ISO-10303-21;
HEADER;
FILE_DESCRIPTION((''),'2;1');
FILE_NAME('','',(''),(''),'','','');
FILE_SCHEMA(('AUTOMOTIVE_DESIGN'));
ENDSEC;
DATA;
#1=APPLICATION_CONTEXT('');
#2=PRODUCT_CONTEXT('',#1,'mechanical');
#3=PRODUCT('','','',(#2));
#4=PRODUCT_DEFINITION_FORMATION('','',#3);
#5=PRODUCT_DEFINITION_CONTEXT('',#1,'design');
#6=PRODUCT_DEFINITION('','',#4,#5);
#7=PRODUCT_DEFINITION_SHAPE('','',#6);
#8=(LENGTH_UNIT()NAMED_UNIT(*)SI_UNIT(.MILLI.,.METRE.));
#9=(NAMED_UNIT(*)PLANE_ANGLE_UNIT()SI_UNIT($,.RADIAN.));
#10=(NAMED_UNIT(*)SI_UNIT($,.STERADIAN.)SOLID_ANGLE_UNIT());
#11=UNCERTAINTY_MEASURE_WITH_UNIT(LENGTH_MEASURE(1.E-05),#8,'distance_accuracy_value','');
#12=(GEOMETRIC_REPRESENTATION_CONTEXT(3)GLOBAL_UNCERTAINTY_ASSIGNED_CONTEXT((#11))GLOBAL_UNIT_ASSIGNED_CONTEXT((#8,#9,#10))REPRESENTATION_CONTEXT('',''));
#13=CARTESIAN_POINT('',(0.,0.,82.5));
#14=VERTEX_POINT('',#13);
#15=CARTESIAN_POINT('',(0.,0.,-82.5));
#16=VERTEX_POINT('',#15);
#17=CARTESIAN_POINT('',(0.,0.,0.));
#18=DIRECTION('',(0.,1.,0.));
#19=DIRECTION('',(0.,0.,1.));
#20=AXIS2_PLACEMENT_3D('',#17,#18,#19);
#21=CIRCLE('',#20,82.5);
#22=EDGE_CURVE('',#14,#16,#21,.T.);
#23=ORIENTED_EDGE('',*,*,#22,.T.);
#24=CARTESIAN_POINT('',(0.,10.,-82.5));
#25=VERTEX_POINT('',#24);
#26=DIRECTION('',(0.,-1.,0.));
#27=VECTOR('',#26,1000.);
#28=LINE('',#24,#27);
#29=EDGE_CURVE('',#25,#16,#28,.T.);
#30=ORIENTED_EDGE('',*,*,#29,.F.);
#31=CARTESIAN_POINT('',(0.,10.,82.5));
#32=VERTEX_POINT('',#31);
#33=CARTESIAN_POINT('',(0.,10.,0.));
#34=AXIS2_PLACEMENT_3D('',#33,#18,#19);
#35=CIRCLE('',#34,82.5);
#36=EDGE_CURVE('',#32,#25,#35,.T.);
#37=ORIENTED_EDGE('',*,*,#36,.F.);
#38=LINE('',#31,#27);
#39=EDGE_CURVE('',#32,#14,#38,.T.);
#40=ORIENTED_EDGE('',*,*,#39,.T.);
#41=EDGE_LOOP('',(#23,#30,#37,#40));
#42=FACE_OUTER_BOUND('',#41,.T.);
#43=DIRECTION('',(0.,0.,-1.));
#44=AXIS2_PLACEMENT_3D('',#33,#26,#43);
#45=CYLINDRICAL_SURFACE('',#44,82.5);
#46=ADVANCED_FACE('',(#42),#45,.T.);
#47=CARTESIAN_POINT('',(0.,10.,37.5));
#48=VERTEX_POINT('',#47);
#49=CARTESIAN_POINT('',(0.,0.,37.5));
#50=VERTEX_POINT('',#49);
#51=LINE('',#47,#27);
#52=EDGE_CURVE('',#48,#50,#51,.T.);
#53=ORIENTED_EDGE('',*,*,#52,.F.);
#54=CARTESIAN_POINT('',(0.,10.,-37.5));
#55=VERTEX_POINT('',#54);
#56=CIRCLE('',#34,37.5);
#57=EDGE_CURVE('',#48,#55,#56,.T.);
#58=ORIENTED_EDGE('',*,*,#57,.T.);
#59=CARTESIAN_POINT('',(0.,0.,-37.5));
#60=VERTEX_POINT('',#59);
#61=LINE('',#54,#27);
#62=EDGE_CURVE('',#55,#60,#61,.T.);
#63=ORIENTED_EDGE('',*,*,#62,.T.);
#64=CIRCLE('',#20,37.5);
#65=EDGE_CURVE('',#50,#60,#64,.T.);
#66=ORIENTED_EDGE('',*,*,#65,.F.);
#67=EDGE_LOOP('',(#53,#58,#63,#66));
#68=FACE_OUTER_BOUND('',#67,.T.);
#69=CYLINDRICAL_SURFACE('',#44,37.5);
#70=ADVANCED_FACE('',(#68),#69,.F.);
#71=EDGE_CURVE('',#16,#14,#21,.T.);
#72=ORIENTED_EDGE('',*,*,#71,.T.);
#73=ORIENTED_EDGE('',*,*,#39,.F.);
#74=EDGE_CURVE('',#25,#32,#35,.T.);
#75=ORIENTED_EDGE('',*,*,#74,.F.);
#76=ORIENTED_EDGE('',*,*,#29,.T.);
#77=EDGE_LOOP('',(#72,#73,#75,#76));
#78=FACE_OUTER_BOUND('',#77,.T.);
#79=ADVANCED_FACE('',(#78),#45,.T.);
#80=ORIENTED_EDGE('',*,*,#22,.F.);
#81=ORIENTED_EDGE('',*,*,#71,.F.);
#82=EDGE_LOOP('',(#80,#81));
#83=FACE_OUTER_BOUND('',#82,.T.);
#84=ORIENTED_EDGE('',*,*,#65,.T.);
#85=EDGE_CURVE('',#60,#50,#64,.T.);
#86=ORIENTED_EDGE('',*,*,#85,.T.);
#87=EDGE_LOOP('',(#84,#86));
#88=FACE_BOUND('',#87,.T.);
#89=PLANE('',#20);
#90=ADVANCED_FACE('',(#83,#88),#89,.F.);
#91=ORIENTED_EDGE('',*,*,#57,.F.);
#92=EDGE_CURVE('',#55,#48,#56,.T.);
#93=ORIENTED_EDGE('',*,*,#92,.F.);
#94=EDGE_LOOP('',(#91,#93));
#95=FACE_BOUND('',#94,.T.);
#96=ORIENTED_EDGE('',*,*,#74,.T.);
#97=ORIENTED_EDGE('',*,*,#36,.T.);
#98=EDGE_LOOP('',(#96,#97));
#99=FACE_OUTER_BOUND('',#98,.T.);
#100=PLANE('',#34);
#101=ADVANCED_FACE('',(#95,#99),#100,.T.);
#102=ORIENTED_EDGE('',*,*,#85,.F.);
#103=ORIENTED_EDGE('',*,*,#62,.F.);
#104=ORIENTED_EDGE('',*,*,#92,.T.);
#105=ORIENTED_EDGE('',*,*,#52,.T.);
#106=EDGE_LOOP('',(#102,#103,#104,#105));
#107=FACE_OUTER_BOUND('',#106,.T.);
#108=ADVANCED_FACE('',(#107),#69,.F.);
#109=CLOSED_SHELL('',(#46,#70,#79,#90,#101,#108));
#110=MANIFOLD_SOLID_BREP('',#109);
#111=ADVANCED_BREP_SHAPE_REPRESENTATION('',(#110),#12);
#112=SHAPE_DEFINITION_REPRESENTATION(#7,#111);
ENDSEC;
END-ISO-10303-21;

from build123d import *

# Parameters (mm, degrees)
WASHER_PROFILE_165_X_75_R   = 82.5
WASHER_PROFILE_165_X_75_R_2 = 37.5
WASHER_BODY_10MM_DEPTH      = 10


with BuildPart() as part:
    # Washer Profile Ø165 x Ø75 → Washer Body 10mm (new body)
    with BuildSketch(Plane(origin=(0, 0, 0), x_dir=(1, 0, 0), z_dir=(0, 1, 0))):
        with Locations(Location((0, 0, 0), (0, 0, 270))):
            Circle(WASHER_PROFILE_165_X_75_R)
        with Locations(Location((0, 0, 0), (0, 0, 270))):
            Circle(WASHER_PROFILE_165_X_75_R_2, mode=Mode.SUBTRACT)
    extrude(amount=WASHER_BODY_10MM_DEPTH)


solid = part.part
